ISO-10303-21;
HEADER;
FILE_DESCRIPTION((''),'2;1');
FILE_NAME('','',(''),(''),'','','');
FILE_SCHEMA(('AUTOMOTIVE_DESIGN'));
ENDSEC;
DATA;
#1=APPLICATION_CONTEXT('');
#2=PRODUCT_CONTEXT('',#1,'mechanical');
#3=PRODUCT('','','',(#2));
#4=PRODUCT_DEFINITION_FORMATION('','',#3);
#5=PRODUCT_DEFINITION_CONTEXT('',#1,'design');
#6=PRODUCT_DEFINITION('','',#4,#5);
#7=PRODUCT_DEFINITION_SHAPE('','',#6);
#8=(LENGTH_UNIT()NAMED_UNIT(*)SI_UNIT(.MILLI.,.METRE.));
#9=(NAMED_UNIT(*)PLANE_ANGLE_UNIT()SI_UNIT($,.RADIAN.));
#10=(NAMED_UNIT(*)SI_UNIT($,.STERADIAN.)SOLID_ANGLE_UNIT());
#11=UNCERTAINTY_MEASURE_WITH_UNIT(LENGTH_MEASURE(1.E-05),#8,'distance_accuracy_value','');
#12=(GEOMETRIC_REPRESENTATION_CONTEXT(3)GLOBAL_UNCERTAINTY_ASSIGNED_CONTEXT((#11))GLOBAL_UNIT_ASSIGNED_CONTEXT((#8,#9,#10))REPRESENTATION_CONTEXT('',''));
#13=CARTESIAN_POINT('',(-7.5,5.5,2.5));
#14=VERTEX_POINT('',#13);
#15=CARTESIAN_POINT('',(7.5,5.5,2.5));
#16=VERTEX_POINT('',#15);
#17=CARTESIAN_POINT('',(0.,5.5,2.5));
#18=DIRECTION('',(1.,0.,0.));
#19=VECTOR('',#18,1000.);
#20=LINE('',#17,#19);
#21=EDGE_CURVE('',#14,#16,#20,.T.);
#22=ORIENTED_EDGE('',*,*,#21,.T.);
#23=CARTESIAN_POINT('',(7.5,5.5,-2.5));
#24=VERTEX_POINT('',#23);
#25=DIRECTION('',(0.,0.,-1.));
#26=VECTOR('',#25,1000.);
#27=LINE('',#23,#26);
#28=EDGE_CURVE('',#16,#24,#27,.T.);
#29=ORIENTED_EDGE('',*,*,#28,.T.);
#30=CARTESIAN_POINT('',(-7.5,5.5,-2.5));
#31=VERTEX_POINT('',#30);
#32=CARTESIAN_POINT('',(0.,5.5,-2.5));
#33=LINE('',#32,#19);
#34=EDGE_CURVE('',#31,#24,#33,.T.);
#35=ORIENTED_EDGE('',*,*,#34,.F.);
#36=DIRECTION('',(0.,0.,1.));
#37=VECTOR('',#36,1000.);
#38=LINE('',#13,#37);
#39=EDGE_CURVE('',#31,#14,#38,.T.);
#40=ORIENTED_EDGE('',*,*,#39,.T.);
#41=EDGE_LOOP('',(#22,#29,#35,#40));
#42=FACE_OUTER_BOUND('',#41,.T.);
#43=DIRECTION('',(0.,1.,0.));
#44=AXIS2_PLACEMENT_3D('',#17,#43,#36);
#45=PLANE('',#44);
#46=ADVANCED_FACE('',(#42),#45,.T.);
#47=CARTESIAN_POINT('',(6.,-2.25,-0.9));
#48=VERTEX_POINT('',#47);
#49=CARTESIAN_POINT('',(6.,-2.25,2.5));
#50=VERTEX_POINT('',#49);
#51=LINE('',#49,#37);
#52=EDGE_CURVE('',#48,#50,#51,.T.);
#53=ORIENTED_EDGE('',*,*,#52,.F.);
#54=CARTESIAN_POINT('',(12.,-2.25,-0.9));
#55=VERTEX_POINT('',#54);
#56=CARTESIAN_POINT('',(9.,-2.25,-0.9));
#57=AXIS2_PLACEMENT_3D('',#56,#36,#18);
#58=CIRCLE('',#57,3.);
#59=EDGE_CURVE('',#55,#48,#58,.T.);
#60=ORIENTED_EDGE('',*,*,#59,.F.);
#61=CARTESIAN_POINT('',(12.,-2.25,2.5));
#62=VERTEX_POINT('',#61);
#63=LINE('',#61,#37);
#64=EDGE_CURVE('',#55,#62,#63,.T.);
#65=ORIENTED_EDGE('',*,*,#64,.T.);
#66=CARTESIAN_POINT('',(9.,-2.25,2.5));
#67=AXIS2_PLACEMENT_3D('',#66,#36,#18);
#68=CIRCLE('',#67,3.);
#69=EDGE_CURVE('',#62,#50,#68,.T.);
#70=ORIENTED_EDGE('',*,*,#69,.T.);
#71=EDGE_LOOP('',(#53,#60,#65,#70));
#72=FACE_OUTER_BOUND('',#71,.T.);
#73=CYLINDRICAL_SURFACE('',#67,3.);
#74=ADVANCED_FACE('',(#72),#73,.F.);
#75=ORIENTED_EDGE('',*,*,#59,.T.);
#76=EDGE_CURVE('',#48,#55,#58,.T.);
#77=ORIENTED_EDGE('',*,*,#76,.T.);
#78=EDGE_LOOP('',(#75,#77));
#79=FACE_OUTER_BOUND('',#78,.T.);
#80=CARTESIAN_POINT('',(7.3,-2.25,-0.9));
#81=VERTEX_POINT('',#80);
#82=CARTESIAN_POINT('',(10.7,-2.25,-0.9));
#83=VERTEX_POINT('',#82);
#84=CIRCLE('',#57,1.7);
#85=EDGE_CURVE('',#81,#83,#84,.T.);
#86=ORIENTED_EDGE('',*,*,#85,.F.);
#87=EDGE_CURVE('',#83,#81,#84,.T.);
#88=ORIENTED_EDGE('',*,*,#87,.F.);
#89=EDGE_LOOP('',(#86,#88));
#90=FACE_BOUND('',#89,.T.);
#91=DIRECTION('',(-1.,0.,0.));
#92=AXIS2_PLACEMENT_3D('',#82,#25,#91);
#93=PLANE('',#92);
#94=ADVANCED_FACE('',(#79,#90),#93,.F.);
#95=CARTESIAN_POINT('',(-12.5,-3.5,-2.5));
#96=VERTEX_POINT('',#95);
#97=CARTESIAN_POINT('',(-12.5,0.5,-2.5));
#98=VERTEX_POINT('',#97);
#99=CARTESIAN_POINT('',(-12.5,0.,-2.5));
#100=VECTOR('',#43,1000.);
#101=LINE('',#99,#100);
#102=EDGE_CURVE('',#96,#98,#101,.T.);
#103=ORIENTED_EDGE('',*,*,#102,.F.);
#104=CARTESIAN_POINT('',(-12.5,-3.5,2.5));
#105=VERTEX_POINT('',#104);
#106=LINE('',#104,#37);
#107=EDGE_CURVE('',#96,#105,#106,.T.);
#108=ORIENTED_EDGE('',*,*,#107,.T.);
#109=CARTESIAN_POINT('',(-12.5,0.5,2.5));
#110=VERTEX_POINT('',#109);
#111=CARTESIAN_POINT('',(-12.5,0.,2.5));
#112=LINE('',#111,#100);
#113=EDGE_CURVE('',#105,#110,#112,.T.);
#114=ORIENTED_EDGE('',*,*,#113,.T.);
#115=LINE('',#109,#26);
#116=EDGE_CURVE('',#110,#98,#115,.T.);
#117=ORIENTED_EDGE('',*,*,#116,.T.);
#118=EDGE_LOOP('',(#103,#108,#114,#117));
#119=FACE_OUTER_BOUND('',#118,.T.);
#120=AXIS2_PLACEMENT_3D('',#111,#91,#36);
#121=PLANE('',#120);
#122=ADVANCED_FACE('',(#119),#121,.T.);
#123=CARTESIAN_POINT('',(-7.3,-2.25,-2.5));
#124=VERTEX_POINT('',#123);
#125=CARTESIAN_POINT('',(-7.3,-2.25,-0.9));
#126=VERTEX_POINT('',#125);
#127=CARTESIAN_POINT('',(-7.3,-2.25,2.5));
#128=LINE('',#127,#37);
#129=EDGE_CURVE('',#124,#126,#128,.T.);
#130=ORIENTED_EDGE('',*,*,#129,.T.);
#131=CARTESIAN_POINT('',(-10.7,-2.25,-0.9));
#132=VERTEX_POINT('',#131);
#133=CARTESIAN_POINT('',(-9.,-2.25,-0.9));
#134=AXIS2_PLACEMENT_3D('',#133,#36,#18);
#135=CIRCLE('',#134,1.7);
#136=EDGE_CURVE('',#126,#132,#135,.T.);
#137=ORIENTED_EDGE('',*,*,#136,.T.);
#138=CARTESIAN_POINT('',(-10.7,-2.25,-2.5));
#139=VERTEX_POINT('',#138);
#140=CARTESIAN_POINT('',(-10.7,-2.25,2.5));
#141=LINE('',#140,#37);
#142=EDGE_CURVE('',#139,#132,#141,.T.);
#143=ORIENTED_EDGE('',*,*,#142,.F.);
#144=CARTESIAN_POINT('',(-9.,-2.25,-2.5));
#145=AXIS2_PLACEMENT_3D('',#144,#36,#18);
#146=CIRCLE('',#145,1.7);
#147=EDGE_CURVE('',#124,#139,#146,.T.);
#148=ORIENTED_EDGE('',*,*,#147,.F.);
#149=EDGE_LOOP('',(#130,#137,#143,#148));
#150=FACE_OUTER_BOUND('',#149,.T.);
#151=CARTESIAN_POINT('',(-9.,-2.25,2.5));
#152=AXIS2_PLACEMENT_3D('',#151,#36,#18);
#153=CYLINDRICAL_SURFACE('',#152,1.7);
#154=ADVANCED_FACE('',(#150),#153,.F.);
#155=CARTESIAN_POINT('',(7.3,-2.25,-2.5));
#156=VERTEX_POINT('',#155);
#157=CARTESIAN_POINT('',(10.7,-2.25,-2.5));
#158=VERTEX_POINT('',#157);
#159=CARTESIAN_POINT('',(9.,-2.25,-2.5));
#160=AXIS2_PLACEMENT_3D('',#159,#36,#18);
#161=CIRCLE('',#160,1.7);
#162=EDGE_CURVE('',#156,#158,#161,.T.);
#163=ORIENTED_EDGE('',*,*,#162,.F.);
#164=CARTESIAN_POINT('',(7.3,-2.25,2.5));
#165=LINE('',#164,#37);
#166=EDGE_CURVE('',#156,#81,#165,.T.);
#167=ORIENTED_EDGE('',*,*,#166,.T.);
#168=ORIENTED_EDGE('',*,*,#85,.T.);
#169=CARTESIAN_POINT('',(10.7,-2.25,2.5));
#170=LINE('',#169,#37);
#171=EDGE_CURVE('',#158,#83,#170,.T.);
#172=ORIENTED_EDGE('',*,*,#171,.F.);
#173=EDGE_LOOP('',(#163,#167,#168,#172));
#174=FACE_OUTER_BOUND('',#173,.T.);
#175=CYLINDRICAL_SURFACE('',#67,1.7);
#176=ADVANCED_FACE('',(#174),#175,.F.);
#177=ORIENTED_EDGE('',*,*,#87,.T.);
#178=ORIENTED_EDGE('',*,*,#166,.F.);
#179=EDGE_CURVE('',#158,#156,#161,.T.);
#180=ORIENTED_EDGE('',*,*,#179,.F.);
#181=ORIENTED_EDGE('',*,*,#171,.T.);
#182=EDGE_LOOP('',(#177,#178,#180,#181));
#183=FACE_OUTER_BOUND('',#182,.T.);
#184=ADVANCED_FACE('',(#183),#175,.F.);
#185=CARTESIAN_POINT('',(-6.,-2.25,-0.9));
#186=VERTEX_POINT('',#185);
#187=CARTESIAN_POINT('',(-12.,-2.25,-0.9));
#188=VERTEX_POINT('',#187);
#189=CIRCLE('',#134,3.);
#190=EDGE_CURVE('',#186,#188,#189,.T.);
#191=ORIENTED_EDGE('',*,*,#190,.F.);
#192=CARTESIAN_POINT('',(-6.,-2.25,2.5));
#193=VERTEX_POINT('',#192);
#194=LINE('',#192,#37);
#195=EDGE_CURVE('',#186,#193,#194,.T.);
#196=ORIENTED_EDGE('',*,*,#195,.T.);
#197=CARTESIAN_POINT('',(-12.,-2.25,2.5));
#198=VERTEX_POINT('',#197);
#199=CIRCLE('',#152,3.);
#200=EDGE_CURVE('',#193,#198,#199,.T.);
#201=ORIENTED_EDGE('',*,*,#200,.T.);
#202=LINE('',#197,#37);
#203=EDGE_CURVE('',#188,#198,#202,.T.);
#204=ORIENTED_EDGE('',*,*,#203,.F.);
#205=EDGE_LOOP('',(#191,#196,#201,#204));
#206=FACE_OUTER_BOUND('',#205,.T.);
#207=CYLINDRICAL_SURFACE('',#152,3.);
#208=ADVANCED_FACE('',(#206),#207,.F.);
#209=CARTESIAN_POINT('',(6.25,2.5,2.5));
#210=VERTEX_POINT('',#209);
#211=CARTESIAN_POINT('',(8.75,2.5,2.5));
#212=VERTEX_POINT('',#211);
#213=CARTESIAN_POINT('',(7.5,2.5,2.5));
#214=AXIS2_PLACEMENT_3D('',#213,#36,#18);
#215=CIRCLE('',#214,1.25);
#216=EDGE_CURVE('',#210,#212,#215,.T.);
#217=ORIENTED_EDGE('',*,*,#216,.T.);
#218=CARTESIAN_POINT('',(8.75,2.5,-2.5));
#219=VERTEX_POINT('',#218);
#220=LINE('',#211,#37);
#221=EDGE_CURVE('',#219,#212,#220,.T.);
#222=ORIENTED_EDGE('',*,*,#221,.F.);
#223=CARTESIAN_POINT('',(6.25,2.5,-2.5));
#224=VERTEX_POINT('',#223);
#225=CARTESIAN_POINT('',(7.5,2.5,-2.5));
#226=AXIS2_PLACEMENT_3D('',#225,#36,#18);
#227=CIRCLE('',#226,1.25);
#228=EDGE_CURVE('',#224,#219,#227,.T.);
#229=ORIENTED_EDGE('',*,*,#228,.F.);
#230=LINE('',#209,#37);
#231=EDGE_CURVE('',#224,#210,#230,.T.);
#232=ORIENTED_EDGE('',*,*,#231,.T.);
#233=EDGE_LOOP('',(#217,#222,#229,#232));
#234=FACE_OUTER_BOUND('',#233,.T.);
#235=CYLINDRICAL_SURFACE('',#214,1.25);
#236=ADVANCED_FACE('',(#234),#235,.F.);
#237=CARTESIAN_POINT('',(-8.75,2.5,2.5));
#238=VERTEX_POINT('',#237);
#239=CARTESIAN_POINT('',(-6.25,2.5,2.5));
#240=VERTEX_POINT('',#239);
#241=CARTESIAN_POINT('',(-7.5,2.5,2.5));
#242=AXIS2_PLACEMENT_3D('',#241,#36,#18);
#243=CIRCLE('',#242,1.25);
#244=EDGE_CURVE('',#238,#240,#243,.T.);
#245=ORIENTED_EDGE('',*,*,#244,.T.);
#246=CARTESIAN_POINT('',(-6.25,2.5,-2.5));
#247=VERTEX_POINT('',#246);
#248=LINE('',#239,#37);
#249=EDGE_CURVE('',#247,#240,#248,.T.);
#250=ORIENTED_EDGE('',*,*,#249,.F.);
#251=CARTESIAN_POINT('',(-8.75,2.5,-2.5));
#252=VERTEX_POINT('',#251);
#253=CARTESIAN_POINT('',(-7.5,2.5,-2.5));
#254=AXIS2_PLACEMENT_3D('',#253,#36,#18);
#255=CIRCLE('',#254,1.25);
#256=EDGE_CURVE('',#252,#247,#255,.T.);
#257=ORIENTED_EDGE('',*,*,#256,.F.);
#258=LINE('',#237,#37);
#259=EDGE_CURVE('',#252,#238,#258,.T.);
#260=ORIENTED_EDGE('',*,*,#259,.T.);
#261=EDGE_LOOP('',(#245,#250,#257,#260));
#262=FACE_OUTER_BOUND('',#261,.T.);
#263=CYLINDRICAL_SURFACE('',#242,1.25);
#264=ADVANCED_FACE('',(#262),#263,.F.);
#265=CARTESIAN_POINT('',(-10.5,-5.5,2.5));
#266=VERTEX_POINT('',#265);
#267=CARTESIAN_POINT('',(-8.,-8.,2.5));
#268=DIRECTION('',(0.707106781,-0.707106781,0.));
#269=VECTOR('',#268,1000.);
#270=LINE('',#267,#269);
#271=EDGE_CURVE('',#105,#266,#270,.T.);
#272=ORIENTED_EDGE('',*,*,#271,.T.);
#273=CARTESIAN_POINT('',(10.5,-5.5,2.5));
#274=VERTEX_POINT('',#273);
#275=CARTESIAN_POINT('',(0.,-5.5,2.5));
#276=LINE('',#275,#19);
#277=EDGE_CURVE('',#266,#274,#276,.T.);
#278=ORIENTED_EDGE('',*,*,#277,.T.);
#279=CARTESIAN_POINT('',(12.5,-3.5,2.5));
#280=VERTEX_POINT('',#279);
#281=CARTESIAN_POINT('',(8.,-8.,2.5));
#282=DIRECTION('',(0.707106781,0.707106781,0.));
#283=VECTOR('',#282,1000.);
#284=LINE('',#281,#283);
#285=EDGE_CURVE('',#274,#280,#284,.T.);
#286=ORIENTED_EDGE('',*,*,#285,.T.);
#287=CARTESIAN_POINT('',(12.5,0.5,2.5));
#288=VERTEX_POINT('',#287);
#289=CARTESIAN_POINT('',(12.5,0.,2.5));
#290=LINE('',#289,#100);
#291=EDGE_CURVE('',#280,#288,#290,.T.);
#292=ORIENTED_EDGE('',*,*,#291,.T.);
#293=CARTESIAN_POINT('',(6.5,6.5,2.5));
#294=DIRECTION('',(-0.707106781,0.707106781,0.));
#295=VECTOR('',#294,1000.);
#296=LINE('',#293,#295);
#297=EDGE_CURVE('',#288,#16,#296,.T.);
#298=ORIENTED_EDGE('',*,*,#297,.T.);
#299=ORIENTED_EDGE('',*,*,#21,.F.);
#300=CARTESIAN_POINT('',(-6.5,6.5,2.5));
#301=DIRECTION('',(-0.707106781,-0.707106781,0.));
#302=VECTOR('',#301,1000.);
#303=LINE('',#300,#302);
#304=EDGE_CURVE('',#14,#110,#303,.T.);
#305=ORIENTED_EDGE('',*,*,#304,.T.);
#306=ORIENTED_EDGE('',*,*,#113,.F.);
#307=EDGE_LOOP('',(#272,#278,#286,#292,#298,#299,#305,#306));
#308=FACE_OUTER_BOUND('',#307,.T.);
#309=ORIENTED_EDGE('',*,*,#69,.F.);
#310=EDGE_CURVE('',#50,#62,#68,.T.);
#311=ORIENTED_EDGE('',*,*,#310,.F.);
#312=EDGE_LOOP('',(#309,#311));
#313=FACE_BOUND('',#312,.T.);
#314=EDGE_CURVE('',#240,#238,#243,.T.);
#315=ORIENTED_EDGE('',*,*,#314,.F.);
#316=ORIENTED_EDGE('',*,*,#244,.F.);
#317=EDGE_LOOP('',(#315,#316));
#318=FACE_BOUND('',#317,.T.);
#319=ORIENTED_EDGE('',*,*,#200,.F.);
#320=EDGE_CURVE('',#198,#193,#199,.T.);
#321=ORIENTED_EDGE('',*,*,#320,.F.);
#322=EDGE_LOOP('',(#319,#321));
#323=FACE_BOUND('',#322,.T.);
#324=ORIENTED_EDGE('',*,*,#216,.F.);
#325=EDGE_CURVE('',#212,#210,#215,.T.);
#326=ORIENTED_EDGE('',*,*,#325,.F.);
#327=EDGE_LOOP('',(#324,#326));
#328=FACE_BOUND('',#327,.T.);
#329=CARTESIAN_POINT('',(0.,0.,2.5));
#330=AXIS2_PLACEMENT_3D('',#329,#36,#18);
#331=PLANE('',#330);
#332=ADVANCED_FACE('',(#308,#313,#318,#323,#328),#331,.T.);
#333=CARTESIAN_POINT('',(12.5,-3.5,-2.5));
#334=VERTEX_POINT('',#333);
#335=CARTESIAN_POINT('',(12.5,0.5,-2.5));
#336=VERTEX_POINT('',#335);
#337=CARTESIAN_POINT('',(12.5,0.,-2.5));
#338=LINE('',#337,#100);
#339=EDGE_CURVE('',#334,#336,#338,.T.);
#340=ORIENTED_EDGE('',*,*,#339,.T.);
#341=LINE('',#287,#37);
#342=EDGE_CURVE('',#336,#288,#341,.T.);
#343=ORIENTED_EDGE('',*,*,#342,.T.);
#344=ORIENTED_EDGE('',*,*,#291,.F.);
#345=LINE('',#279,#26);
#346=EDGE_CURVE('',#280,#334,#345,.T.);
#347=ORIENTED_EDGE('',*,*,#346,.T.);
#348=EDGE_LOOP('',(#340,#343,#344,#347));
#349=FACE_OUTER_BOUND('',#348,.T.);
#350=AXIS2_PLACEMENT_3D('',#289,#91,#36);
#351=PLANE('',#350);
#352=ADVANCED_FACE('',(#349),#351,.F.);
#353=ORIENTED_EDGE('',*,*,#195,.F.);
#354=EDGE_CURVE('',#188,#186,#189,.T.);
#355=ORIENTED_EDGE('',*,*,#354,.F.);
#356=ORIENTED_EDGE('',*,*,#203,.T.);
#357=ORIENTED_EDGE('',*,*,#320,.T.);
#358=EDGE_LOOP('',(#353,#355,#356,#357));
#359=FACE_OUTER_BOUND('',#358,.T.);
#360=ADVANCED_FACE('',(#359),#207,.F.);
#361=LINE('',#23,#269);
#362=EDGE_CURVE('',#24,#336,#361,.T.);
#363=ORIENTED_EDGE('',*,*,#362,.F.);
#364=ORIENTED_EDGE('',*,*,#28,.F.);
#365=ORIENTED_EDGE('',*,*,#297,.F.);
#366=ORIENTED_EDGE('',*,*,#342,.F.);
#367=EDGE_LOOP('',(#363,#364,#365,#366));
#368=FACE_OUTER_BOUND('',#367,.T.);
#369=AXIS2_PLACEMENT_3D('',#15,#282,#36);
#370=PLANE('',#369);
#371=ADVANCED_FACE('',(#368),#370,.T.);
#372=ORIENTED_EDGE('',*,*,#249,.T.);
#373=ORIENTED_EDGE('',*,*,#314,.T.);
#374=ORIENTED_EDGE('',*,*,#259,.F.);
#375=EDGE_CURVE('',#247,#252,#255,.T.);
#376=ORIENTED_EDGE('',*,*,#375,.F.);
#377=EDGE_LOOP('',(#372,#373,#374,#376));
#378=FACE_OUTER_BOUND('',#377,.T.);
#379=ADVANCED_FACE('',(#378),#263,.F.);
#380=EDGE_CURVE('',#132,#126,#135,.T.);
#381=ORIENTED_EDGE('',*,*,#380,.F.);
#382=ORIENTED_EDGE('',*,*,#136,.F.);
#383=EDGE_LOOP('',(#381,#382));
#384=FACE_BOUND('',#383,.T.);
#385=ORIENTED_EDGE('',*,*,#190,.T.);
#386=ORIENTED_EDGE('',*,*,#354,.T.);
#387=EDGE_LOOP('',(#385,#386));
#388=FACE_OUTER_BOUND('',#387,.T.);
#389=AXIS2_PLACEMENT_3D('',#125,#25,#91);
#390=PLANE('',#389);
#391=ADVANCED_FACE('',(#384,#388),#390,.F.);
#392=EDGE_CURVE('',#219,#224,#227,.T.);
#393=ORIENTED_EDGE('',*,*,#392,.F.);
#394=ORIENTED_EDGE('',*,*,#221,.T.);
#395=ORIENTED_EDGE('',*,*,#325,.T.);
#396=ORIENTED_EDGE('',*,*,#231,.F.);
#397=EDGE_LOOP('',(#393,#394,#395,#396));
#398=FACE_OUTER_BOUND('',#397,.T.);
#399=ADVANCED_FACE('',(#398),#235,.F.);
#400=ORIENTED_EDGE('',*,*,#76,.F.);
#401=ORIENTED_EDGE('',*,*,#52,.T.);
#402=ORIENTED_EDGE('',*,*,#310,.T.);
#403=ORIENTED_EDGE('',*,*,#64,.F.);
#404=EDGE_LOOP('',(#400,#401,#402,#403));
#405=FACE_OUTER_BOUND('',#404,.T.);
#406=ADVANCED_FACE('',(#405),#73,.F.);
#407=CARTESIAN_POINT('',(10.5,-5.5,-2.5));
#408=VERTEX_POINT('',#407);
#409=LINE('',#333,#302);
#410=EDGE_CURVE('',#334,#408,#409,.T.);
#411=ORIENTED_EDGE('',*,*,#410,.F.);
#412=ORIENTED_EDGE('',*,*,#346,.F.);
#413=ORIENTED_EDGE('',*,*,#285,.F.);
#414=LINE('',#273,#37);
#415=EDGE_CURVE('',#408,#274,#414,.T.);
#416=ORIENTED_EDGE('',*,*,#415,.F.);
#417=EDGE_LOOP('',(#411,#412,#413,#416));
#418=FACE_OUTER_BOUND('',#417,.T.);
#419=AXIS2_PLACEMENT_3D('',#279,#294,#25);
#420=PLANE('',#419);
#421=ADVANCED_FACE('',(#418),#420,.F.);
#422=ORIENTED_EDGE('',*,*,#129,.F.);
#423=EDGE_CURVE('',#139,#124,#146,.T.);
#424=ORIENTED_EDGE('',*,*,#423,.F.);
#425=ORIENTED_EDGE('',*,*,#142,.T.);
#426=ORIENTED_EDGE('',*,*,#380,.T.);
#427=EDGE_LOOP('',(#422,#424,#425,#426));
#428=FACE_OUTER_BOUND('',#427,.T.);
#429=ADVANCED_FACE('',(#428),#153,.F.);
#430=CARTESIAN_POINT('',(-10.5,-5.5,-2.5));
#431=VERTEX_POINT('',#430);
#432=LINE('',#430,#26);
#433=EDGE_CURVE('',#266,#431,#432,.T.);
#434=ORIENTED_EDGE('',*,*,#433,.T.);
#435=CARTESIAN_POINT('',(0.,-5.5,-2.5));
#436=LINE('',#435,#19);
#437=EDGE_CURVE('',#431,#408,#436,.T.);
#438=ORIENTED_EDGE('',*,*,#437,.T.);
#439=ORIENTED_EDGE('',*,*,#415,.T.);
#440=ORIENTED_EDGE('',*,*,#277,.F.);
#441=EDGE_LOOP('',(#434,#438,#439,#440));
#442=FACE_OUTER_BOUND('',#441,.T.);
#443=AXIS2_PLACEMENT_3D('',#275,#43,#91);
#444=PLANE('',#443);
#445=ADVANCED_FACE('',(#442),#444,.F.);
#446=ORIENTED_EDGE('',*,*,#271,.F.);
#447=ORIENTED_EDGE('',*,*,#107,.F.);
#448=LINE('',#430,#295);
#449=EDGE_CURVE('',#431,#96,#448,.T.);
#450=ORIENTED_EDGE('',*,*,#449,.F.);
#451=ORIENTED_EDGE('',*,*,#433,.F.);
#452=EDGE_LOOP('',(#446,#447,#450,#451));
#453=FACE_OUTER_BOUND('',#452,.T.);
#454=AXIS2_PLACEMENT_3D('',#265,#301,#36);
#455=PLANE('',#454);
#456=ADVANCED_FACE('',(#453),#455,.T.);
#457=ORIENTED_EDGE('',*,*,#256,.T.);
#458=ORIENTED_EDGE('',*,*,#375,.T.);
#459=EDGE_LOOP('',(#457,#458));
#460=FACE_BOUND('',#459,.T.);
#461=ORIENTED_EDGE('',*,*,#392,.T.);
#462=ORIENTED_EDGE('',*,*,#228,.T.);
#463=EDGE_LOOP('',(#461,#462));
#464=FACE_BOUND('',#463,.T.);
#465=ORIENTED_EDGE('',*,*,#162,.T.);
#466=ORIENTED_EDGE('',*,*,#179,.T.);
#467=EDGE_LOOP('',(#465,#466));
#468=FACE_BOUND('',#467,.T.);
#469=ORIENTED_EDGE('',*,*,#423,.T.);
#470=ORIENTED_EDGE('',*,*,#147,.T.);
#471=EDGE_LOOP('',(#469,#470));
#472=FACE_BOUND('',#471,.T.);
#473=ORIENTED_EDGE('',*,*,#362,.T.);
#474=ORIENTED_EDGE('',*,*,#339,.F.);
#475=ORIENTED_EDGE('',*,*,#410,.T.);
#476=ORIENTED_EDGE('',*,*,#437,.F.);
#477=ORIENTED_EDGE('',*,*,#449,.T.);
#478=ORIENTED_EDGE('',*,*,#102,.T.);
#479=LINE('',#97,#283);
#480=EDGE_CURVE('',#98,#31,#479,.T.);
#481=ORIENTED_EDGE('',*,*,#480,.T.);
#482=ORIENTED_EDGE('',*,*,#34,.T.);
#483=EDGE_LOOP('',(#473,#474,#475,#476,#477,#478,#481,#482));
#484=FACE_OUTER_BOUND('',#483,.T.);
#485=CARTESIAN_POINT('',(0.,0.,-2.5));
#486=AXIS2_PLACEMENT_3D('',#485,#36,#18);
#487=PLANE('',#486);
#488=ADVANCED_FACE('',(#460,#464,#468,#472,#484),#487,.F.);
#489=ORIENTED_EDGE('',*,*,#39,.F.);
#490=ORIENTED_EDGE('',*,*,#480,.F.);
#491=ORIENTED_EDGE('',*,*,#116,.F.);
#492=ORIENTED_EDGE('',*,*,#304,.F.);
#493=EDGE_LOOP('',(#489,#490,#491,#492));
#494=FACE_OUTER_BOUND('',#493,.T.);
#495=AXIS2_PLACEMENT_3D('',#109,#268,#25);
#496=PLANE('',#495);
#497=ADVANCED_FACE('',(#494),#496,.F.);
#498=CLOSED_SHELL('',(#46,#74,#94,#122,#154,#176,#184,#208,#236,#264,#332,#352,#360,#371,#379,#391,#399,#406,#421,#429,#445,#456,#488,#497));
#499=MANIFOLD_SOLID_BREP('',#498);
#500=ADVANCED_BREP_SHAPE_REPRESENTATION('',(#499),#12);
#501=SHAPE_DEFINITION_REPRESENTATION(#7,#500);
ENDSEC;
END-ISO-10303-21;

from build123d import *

# Parameters (mm, degrees)
SKETCH1_W                                           = 8.5
SKETCH1_H                                           = 3.5
BOSS_EXTRUDE1_DEPTH                                 = 2.5
M3_TAPPED_HOLE1_D                                   = 2.5
HOLE_SIZE_BY_SOCKET_HEAD_CAP_SCREW_TYPE_D           = 3.4
HOLE_SIZE_BY_SOCKET_HEAD_CAP_SCREW_TYPE_CBORE_D     = 6
HOLE_SIZE_BY_SOCKET_HEAD_CAP_SCREW_TYPE_CBORE_DEPTH = 3.4
CHAMFER2_SIZE                                       = 5
CHAMFER3_SIZE                                       = 2


with BuildPart() as part:
    # Sketch1 → Boss-Extrude1 (new, symmetric)
    with BuildSketch(Plane.XY):
        Polygon((-12.5, 2), (-12.5, -5.5), (12.5, -5.5), (12.5, 2), (4, 2), (4, 5.5), (-4, 5.5), (-4, 2), align=None)
        with Locations((8.25, 3.75)):
            Rectangle(SKETCH1_W, SKETCH1_H)
        with Locations((-8.25, 3.75)):
            Rectangle(SKETCH1_W, SKETCH1_H)
    extrude(amount=BOSS_EXTRUDE1_DEPTH, both=True)

    # M3 Tapped Hole1 (through all)
    with Locations(Plane.XY.offset(2.5)):
        with Locations((-7.5, 2.5), (7.5, 2.5)):
            Hole(M3_TAPPED_HOLE1_D / 2)

    # Hole size (by socket head cap screw type)1 (through all)
    with Locations(Plane.XY.offset(2.5)):
        with Locations((9, -2.25), (-9, -2.25)):
            CounterBoreHole(HOLE_SIZE_BY_SOCKET_HEAD_CAP_SCREW_TYPE_D / 2, HOLE_SIZE_BY_SOCKET_HEAD_CAP_SCREW_TYPE_CBORE_D / 2, HOLE_SIZE_BY_SOCKET_HEAD_CAP_SCREW_TYPE_CBORE_DEPTH)

    # Chamfer2
    chamfer2_edges = [part.edges().sort_by_distance(p)[0] for p in [
        (12.5, 5.5, 0),
        (-12.5, 5.5, 0),
    ]]
    chamfer(chamfer2_edges, length=CHAMFER2_SIZE)

    # Chamfer3
    chamfer3_edges = [part.edges().sort_by_distance(p)[0] for p in [
        (12.5, -5.5, 0),
        (-12.5, -5.5, 0),
    ]]
    chamfer(chamfer3_edges, length=CHAMFER3_SIZE)


solid = part.part
